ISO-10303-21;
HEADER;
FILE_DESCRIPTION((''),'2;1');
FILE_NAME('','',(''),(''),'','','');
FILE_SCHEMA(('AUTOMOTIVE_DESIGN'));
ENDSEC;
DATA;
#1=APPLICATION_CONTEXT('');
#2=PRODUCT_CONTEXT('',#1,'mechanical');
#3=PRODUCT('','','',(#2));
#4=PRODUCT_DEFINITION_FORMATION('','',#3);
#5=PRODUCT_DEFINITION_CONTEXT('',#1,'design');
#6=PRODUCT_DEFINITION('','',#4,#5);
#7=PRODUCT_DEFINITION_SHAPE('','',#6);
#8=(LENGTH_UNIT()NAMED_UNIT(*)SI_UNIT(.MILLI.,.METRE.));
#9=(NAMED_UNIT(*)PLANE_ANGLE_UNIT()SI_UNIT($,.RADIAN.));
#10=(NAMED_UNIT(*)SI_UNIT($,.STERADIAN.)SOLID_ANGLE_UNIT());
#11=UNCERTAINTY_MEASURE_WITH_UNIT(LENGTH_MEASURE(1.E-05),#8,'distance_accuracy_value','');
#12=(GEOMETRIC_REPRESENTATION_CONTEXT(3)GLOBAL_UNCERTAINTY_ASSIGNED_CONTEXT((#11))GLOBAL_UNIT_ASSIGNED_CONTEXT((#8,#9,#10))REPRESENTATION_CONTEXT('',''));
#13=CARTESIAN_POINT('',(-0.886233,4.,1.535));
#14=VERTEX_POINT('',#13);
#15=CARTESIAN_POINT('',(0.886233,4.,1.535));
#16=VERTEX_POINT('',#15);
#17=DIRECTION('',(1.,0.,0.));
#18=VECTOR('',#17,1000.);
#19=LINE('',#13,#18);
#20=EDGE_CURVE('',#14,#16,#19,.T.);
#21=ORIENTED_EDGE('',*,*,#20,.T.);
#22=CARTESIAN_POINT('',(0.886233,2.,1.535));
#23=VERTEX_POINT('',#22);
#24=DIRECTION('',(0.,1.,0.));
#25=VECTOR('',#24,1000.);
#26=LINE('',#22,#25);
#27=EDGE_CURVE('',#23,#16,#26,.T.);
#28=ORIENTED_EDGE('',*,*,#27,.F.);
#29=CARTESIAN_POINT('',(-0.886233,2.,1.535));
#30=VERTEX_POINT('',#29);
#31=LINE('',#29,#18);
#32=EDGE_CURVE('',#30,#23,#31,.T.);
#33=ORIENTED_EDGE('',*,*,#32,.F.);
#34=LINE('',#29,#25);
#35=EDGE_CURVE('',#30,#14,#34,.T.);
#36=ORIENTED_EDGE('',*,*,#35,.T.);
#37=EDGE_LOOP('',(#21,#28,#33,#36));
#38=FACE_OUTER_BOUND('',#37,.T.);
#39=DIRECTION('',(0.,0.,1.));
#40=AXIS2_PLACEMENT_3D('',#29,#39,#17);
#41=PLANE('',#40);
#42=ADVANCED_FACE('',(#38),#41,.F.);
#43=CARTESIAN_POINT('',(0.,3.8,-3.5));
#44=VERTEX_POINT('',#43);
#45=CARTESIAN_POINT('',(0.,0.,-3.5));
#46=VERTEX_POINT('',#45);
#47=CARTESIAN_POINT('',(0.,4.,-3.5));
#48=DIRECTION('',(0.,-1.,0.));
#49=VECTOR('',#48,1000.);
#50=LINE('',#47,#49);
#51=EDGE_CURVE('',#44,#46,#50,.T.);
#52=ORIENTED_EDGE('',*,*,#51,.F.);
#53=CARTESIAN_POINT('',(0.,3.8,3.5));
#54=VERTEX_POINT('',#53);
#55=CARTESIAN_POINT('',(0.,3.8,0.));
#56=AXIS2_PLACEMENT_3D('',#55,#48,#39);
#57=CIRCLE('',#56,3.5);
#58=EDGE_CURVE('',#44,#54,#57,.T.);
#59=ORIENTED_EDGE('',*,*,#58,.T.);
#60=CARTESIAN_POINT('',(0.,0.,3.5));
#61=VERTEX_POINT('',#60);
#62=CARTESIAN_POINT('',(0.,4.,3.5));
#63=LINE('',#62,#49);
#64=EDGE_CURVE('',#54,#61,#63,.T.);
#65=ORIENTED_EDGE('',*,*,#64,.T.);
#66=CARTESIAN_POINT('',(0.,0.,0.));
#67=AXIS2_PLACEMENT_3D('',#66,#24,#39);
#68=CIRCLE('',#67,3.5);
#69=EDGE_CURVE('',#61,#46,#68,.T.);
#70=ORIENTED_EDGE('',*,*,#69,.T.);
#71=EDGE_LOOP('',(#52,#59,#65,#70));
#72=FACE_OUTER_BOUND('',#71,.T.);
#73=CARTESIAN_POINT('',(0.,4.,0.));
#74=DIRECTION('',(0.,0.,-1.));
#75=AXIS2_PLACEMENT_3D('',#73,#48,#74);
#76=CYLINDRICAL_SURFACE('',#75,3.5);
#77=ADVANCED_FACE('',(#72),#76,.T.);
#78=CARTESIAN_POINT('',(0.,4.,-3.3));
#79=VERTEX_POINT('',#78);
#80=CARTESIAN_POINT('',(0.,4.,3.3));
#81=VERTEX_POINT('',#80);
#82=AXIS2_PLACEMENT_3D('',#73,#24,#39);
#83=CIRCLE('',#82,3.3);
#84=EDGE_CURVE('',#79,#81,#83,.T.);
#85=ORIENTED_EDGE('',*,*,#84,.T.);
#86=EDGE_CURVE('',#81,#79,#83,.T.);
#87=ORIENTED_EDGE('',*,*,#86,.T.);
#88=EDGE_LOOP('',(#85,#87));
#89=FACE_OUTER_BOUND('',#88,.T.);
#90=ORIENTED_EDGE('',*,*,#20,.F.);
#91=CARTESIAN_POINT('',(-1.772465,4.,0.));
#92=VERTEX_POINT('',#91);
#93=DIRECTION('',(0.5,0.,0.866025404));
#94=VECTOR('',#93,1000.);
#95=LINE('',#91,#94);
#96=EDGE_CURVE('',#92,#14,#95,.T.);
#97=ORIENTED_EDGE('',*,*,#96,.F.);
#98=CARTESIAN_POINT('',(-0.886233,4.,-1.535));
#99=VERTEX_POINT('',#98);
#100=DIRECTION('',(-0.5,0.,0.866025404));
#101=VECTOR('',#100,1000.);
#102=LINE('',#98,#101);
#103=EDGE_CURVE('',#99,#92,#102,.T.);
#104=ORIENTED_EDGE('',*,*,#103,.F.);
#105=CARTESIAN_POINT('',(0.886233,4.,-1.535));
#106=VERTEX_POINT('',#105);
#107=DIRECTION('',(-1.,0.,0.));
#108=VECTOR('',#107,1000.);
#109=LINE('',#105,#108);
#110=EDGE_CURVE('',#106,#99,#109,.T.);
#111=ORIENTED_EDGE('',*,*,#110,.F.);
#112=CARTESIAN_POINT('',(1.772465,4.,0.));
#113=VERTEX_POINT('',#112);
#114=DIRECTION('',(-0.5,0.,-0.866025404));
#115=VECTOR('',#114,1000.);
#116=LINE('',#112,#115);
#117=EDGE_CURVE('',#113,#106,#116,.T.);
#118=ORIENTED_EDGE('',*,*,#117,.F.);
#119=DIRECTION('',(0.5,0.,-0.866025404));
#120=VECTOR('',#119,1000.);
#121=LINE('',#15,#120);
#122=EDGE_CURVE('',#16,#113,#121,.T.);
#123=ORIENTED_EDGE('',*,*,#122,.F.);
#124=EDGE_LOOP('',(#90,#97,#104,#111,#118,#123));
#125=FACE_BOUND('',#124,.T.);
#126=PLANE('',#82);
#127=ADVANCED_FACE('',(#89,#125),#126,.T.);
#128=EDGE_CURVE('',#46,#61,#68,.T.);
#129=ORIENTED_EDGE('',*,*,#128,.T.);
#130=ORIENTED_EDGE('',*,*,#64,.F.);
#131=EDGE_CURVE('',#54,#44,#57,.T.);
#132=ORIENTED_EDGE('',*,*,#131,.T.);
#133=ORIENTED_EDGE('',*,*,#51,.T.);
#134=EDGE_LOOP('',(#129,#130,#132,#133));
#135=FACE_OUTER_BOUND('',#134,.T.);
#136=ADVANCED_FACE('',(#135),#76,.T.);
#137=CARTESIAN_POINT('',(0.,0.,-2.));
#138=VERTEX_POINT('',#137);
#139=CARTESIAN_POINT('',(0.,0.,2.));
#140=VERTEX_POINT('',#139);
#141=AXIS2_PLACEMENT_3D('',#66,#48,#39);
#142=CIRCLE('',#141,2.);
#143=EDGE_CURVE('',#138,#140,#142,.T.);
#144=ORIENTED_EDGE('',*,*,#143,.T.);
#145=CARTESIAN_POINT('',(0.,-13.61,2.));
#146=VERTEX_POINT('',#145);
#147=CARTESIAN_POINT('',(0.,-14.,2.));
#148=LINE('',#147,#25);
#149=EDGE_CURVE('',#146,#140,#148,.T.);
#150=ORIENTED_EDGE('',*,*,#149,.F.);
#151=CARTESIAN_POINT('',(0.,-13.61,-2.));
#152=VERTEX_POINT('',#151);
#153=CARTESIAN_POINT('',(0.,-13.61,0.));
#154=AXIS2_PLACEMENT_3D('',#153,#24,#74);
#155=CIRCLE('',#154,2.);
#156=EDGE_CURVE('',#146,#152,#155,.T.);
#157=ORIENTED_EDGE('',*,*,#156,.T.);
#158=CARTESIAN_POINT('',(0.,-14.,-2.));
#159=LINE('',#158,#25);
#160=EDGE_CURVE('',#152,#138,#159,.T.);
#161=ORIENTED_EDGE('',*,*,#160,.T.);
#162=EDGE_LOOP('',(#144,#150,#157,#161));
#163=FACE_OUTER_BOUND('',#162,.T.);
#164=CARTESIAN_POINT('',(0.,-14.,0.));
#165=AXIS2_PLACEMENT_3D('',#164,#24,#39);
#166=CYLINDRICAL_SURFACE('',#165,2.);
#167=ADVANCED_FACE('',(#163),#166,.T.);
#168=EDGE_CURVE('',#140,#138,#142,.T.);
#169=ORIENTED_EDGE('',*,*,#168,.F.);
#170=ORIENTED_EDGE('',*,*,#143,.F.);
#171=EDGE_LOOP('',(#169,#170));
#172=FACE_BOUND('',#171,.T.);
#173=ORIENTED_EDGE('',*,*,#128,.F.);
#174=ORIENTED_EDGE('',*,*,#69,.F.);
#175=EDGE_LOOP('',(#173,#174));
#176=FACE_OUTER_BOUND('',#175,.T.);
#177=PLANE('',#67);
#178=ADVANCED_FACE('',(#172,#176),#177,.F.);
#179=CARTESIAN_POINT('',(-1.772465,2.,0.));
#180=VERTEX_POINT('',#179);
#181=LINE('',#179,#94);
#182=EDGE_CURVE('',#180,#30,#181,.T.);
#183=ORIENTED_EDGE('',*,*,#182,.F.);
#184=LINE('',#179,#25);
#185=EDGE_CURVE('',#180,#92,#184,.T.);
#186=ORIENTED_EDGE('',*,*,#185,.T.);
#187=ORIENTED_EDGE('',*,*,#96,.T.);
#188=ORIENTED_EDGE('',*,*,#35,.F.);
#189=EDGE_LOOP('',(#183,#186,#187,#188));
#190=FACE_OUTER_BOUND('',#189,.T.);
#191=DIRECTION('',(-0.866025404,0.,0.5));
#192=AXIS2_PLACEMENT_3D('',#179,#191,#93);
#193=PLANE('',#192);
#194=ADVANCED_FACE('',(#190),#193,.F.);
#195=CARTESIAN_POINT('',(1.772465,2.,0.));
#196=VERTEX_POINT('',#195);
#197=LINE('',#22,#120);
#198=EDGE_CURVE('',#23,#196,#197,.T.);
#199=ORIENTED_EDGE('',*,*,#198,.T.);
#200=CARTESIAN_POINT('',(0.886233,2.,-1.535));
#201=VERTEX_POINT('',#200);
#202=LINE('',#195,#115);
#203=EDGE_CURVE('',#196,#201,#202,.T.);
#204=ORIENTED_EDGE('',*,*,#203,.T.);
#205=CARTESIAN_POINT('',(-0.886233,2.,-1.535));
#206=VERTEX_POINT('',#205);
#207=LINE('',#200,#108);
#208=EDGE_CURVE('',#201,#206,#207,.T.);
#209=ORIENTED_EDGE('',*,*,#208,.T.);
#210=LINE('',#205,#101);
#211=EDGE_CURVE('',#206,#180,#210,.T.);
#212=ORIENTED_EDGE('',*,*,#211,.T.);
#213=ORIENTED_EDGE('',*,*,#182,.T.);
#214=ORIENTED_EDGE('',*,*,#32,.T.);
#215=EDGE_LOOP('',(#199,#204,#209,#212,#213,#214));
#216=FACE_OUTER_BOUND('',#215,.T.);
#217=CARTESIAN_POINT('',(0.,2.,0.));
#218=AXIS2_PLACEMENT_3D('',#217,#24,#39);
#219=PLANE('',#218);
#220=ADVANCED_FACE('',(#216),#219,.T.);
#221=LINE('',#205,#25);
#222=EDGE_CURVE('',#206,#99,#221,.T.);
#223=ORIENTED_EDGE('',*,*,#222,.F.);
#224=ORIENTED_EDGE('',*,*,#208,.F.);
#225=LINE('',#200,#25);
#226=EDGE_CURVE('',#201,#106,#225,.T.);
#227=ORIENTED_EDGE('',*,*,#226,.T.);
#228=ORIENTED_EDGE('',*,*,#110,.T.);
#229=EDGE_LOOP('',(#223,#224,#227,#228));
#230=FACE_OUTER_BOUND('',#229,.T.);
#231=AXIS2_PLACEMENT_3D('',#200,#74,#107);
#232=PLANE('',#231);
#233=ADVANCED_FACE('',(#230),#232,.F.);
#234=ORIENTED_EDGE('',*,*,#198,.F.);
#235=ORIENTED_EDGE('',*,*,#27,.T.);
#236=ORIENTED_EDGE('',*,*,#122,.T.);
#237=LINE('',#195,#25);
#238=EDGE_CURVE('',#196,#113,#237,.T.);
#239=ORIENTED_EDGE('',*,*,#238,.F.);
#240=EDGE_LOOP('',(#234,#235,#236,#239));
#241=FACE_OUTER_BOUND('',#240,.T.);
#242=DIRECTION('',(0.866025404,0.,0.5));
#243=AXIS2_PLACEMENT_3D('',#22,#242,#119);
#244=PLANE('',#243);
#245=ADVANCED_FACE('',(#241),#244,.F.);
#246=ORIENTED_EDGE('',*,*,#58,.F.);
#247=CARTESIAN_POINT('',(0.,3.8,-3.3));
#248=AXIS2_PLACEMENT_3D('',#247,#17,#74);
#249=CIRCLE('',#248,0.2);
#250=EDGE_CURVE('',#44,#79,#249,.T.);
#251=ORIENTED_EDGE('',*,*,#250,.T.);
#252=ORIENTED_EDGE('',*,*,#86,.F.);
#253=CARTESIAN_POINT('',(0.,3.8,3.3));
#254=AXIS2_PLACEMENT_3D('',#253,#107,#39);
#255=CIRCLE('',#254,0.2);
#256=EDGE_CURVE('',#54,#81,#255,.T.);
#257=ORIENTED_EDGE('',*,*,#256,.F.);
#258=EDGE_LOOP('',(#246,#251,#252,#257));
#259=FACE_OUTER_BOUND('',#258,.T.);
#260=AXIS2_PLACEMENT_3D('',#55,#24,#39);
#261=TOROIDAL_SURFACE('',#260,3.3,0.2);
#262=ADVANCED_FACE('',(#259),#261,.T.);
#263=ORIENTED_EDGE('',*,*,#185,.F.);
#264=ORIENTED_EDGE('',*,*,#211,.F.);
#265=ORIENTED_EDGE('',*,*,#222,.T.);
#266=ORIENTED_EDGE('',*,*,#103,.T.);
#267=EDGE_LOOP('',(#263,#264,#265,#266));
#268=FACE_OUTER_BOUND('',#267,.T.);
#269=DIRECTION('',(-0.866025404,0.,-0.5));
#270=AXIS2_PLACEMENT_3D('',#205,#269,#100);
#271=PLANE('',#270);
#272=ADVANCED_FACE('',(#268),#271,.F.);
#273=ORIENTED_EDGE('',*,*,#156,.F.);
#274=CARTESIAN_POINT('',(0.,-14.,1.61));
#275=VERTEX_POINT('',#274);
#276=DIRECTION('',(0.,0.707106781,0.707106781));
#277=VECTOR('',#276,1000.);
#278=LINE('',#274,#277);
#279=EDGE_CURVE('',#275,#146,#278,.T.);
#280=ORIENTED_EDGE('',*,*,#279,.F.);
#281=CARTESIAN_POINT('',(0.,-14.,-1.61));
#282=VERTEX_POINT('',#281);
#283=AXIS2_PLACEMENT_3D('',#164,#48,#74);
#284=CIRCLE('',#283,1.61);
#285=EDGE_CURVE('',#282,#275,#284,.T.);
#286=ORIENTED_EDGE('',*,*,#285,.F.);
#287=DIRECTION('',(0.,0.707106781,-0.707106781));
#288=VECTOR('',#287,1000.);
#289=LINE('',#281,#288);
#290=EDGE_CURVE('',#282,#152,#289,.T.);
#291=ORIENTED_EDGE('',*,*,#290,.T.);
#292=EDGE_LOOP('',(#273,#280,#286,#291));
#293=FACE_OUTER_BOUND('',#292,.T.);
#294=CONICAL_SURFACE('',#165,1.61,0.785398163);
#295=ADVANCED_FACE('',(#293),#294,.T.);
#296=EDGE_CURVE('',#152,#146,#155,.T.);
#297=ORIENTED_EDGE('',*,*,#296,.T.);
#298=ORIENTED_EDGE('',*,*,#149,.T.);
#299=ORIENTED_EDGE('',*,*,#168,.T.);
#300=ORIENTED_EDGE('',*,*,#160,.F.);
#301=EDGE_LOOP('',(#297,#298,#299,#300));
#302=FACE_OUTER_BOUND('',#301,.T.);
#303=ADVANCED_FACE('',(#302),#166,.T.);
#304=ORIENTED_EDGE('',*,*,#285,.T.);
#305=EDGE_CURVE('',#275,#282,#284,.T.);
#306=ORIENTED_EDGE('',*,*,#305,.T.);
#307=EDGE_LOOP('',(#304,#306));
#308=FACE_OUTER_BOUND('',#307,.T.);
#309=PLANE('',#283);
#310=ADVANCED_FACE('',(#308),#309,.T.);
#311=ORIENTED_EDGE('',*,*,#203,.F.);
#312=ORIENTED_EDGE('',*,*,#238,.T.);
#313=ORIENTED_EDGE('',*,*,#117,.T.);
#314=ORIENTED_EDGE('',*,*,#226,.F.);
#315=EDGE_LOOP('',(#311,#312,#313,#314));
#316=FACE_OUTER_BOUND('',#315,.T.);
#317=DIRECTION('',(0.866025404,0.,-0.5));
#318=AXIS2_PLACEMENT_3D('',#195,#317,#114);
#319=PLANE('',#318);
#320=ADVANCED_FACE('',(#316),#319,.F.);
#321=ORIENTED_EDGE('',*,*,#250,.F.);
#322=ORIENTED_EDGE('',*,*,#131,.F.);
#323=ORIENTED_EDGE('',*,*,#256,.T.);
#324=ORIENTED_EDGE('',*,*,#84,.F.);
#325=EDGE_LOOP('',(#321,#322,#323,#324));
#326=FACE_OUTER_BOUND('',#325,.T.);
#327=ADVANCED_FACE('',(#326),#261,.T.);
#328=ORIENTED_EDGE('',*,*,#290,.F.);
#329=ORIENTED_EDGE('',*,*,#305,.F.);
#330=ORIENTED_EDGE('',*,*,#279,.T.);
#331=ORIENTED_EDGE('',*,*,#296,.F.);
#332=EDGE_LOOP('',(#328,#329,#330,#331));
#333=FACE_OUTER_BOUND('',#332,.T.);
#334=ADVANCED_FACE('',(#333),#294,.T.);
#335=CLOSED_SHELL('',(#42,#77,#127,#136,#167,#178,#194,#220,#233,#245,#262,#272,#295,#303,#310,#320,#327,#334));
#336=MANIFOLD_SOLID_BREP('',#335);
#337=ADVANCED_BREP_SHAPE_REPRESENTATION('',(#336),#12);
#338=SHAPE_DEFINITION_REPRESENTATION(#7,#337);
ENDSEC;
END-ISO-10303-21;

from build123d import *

# Parameters (mm, degrees)
SKETCH_1_R          = 3.5
EXTRUDE_1_DEPTH     = 4
CUT_EXTRUDE_1_DEPTH = 2
FILLET_1_R          = 0.2
SKETCH_5_R          = 2
EXTRUDE_2_DEPTH     = 14
CHAMFER_2_SIZE      = 0.39


with BuildPart() as part:
    # 草图1 → 凸台-拉伸1 (new body)
    with BuildSketch(Plane(origin=(0, 0, 0), x_dir=(1, 0, 0), z_dir=(0, 1, 0))):
        with Locations(Location((0, 0, 0), (0, 0, 270))):
            Circle(SKETCH_1_R)
    extrude(amount=EXTRUDE_1_DEPTH)

    # 草图2 → 切除-拉伸1 (cut)
    with BuildSketch(Plane(origin=(0, 4, 0), x_dir=(1, 0, 0), z_dir=(0, 1, 0))):
        Polygon((1.772465326, 0), (0.886232663, 1.535), (-0.886232663, 1.535), (-1.772465326, 0), (-0.886232663, -1.535), (0.886232663, -1.535), align=None)
    extrude(amount=-CUT_EXTRUDE_1_DEPTH, mode=Mode.SUBTRACT)

    # 圆角1
    fillet_1_edges = [part.edges().sort_by_distance(p)[0] for p in [
        (0, 4, -3.5),
    ]]
    fillet(fillet_1_edges, radius=FILLET_1_R)

    # 草图5 → 凸台-拉伸2 (add)
    with BuildSketch(Plane.XZ):
        with Locations(Location((0, 0, 0), (0, 0, 90))):
            Circle(SKETCH_5_R)
    extrude(amount=EXTRUDE_2_DEPTH)

    # 倒角2
    chamfer_2_edges = [part.edges().sort_by_distance(p)[0] for p in [
        (0, -14, -2),
    ]]
    chamfer(chamfer_2_edges, length=CHAMFER_2_SIZE)


solid = part.part
